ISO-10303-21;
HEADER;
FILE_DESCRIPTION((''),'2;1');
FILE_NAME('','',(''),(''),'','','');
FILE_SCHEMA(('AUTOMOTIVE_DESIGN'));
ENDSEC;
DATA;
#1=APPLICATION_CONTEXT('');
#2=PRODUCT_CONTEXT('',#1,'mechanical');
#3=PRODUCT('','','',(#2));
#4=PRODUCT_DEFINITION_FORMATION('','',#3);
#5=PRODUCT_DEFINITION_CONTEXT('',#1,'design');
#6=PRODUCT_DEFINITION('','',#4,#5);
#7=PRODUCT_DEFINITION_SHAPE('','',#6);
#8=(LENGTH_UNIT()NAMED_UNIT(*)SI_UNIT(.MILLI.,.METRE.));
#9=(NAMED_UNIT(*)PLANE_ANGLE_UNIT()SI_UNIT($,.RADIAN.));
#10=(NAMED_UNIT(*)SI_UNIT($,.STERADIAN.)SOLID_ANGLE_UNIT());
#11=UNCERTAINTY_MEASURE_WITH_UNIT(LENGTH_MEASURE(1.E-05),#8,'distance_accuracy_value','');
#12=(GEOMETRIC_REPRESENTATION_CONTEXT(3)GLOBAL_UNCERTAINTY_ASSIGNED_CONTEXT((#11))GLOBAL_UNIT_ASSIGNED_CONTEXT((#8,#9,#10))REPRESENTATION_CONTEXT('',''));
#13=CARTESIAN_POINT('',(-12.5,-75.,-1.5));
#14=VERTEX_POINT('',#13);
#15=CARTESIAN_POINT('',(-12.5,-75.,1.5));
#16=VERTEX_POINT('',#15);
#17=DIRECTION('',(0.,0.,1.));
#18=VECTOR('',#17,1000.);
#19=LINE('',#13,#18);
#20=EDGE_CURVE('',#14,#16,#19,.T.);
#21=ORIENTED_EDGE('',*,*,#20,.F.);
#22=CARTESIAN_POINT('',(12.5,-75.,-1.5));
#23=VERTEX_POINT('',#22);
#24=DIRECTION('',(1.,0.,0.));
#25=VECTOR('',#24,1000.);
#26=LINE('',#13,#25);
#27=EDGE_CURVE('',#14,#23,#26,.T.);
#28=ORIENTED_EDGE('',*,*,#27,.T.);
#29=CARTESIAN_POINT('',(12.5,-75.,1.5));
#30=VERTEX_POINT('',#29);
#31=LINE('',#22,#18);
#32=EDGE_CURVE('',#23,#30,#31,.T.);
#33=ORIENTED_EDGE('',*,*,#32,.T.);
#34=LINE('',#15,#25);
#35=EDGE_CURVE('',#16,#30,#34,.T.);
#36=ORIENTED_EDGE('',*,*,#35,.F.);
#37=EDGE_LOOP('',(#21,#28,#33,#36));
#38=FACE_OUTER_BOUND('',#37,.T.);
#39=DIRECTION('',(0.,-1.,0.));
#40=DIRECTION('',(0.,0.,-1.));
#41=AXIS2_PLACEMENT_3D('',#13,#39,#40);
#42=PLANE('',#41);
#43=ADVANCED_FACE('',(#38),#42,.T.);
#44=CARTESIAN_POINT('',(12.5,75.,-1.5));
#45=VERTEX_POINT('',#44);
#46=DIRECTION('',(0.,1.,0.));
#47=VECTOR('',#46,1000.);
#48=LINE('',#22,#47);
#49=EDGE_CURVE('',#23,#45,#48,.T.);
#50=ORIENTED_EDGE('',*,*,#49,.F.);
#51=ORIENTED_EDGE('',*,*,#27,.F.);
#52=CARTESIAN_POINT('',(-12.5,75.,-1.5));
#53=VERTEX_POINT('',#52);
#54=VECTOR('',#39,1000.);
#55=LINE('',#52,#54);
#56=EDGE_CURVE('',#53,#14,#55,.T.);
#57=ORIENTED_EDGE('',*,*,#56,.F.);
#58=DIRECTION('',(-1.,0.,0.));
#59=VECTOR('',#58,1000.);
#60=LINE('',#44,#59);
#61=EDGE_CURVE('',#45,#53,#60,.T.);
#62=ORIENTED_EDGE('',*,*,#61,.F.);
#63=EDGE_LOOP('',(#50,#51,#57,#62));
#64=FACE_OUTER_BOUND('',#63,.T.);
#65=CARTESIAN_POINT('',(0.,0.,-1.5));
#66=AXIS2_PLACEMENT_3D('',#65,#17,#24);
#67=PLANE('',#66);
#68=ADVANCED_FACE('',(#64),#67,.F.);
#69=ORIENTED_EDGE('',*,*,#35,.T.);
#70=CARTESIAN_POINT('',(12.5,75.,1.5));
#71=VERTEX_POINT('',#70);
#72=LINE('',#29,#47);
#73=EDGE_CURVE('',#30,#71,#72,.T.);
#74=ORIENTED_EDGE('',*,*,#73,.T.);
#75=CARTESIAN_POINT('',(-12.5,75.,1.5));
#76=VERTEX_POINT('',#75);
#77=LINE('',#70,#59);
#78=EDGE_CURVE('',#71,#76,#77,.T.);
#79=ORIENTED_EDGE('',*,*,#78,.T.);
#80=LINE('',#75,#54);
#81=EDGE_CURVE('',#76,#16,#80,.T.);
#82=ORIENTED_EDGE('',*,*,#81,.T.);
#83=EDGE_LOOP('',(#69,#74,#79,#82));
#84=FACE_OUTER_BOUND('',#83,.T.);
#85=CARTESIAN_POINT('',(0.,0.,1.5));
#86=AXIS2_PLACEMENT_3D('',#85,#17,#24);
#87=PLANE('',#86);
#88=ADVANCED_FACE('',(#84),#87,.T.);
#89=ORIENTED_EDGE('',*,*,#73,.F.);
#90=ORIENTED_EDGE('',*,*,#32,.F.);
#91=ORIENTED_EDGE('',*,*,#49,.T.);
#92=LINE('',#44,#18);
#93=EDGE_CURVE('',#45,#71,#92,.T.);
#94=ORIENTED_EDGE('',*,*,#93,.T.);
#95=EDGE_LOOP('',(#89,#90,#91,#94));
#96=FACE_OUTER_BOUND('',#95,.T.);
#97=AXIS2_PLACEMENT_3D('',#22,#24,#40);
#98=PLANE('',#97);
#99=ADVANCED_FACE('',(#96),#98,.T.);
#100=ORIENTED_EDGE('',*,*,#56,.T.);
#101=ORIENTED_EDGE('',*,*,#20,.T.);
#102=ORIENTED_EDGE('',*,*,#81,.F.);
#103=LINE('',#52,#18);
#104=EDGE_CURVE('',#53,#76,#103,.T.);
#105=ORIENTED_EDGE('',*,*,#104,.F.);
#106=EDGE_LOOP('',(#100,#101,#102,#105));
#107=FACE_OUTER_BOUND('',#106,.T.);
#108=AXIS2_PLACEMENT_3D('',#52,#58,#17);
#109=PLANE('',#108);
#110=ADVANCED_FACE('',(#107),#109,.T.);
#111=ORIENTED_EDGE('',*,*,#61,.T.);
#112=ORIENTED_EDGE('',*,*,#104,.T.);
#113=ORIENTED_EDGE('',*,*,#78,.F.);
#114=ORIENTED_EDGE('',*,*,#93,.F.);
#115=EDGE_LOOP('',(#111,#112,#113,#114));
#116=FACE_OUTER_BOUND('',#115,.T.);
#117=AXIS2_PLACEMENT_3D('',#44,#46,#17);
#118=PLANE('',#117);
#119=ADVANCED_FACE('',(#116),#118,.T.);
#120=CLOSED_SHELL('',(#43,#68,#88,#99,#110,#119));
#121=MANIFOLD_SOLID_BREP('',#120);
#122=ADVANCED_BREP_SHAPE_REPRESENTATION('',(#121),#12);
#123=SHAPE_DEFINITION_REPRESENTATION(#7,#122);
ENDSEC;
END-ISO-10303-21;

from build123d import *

# Parameters (mm, degrees)
SKETCH_1_W      = 25
SKETCH_1_H      = 150
EXTRUDE_1_DEPTH = 1.5


with BuildPart() as part:
    # 草图1 → 凸台-拉伸1 (new, symmetric)
    with BuildSketch(Plane.XY):
        Rectangle(SKETCH_1_W, SKETCH_1_H)
    extrude(amount=EXTRUDE_1_DEPTH, both=True)


solid = part.part
